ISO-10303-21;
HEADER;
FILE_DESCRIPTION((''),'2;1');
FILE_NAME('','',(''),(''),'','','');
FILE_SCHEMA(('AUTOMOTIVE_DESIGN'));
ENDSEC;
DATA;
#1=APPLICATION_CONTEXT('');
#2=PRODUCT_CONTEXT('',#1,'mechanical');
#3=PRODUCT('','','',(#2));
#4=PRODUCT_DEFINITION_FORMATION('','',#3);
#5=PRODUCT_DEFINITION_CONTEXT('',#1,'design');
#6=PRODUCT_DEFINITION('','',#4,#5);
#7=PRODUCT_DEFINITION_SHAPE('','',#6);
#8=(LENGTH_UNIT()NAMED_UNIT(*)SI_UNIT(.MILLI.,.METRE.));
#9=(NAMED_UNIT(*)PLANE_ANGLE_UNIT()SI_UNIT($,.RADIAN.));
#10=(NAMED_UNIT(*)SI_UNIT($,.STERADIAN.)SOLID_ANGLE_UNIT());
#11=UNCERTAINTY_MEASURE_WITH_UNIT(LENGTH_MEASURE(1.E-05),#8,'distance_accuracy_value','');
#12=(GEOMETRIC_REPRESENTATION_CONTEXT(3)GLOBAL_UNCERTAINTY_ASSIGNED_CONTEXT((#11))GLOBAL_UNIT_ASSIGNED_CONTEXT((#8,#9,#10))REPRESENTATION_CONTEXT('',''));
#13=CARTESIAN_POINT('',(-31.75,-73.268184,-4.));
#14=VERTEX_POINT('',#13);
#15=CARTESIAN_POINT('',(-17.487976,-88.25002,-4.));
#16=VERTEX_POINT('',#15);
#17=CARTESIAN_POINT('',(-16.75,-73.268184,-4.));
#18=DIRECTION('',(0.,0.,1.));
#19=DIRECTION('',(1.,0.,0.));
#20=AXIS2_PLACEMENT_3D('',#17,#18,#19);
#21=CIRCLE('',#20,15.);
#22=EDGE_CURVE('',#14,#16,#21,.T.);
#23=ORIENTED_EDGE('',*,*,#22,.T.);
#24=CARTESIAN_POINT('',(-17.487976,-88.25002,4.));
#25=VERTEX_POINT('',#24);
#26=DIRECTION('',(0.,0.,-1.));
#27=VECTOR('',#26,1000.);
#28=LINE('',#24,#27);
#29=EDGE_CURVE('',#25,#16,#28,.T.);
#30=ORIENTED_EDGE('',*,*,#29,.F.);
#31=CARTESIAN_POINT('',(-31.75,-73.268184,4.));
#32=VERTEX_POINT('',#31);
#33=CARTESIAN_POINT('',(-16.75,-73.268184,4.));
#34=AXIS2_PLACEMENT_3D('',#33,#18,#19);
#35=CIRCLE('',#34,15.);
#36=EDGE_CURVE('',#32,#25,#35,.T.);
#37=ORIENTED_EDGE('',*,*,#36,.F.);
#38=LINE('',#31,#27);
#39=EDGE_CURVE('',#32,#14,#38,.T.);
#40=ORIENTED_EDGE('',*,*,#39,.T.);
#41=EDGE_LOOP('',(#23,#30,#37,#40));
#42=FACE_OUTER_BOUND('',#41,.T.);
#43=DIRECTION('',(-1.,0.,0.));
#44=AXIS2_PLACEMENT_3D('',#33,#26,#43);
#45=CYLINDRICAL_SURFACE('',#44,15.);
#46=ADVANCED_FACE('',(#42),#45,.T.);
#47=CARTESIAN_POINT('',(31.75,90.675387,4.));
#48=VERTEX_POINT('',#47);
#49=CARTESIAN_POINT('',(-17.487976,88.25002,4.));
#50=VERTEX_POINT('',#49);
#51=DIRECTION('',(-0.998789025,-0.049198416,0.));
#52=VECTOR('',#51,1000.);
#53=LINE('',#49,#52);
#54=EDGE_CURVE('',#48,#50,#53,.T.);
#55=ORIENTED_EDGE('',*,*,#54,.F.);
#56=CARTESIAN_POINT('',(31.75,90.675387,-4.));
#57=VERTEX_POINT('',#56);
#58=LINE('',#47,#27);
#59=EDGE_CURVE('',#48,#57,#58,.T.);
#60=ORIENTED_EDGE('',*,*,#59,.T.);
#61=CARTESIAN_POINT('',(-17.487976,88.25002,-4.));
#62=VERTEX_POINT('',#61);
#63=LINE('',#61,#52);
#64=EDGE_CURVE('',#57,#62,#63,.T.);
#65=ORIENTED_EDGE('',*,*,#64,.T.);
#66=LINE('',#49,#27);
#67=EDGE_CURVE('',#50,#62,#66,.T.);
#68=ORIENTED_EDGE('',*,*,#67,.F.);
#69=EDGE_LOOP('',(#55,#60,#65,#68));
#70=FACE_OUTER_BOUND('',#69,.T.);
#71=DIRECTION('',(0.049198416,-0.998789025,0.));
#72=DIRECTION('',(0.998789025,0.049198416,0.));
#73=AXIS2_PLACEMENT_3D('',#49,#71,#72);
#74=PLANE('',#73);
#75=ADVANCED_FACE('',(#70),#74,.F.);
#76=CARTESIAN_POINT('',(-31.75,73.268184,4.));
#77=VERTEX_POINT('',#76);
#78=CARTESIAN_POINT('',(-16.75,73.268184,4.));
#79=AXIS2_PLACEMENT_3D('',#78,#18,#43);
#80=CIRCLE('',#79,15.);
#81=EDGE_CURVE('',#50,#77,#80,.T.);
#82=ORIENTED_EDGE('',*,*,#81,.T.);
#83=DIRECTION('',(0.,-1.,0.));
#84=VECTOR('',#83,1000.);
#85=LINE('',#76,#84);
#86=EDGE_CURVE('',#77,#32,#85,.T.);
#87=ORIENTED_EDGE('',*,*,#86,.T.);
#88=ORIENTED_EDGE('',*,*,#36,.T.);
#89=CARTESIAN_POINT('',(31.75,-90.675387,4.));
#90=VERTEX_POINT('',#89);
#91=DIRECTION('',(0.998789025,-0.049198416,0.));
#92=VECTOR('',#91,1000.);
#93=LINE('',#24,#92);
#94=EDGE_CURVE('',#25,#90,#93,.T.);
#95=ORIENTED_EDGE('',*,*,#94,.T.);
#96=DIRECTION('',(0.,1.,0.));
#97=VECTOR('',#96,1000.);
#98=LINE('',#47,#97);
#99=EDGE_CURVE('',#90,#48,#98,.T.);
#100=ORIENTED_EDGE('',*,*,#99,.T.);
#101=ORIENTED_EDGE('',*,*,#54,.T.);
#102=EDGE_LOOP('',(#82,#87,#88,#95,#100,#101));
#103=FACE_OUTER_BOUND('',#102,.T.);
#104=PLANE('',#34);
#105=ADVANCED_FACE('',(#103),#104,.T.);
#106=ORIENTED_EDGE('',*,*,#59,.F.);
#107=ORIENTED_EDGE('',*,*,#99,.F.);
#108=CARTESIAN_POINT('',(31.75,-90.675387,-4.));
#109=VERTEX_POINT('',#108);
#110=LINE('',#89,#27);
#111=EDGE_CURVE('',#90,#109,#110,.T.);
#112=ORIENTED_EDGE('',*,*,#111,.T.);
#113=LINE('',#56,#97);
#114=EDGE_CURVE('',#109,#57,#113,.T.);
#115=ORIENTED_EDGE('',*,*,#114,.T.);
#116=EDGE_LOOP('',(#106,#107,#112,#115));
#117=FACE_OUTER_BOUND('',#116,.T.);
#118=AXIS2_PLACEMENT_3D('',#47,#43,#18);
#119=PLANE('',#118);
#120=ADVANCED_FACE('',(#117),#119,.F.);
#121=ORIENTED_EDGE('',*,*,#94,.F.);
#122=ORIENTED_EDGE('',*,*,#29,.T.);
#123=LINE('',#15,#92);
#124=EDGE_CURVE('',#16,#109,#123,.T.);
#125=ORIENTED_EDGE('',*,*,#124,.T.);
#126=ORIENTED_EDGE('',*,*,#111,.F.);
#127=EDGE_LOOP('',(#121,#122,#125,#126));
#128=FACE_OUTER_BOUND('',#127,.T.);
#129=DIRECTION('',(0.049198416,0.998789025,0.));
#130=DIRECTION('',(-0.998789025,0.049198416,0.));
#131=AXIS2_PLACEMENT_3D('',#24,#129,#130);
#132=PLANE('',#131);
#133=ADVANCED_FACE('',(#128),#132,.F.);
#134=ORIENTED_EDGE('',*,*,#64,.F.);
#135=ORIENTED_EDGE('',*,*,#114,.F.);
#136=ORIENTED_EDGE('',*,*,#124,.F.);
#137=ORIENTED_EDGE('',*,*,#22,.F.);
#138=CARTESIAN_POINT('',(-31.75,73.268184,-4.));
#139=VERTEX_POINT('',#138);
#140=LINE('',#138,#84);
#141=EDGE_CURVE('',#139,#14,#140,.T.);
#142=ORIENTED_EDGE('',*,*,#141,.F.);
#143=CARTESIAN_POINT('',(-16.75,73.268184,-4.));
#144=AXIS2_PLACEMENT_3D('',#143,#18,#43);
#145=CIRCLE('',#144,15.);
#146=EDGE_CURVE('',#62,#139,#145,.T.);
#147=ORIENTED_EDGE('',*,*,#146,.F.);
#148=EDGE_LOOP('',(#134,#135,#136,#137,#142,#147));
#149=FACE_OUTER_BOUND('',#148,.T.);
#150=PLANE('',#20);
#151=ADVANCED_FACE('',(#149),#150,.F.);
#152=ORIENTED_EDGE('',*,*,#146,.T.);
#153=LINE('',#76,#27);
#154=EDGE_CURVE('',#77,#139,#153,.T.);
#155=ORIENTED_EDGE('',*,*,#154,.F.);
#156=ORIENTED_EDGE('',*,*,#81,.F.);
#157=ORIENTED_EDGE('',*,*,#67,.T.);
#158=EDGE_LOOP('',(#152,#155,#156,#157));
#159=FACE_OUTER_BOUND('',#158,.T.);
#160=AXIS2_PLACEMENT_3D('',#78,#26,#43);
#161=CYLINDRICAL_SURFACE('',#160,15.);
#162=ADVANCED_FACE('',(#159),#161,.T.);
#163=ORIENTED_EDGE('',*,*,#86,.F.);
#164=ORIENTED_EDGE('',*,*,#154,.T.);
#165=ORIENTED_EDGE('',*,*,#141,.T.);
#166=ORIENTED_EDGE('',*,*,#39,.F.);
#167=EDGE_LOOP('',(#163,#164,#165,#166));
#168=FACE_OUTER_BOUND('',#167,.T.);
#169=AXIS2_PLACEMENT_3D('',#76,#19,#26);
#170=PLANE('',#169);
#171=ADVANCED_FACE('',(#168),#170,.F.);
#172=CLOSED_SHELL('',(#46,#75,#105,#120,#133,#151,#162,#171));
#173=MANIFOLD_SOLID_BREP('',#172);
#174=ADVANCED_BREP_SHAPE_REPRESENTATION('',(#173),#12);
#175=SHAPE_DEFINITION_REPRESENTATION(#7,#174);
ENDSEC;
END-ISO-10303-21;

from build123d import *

# Parameters (mm, degrees)
BOSS_EXTRUDE1_DEPTH = 4


with BuildPart() as part:
    # Sketch1 → Boss-Extrude1 (new, symmetric)
    with BuildSketch(Plane.XY):
        with BuildLine():
            Line((-31.75, 73.26818434), (-31.75, -73.26818434))
            ThreePointArc((-31.75, -73.26818434), (-27.614383176, -83.610581461), (-17.487976239, -88.250019711))
            Line((-17.487976239, -88.250019711), (31.75, -90.675387205))
            Line((31.75, -90.675387205), (31.75, 90.675387205))
            Line((31.75, 90.675387205), (-17.487976239, 88.250019711))
            ThreePointArc((-17.487976239, 88.250019711), (-27.614383176, 83.610581461), (-31.75, 73.26818434))
        make_face()
    extrude(amount=BOSS_EXTRUDE1_DEPTH, both=True)


solid = part.part
